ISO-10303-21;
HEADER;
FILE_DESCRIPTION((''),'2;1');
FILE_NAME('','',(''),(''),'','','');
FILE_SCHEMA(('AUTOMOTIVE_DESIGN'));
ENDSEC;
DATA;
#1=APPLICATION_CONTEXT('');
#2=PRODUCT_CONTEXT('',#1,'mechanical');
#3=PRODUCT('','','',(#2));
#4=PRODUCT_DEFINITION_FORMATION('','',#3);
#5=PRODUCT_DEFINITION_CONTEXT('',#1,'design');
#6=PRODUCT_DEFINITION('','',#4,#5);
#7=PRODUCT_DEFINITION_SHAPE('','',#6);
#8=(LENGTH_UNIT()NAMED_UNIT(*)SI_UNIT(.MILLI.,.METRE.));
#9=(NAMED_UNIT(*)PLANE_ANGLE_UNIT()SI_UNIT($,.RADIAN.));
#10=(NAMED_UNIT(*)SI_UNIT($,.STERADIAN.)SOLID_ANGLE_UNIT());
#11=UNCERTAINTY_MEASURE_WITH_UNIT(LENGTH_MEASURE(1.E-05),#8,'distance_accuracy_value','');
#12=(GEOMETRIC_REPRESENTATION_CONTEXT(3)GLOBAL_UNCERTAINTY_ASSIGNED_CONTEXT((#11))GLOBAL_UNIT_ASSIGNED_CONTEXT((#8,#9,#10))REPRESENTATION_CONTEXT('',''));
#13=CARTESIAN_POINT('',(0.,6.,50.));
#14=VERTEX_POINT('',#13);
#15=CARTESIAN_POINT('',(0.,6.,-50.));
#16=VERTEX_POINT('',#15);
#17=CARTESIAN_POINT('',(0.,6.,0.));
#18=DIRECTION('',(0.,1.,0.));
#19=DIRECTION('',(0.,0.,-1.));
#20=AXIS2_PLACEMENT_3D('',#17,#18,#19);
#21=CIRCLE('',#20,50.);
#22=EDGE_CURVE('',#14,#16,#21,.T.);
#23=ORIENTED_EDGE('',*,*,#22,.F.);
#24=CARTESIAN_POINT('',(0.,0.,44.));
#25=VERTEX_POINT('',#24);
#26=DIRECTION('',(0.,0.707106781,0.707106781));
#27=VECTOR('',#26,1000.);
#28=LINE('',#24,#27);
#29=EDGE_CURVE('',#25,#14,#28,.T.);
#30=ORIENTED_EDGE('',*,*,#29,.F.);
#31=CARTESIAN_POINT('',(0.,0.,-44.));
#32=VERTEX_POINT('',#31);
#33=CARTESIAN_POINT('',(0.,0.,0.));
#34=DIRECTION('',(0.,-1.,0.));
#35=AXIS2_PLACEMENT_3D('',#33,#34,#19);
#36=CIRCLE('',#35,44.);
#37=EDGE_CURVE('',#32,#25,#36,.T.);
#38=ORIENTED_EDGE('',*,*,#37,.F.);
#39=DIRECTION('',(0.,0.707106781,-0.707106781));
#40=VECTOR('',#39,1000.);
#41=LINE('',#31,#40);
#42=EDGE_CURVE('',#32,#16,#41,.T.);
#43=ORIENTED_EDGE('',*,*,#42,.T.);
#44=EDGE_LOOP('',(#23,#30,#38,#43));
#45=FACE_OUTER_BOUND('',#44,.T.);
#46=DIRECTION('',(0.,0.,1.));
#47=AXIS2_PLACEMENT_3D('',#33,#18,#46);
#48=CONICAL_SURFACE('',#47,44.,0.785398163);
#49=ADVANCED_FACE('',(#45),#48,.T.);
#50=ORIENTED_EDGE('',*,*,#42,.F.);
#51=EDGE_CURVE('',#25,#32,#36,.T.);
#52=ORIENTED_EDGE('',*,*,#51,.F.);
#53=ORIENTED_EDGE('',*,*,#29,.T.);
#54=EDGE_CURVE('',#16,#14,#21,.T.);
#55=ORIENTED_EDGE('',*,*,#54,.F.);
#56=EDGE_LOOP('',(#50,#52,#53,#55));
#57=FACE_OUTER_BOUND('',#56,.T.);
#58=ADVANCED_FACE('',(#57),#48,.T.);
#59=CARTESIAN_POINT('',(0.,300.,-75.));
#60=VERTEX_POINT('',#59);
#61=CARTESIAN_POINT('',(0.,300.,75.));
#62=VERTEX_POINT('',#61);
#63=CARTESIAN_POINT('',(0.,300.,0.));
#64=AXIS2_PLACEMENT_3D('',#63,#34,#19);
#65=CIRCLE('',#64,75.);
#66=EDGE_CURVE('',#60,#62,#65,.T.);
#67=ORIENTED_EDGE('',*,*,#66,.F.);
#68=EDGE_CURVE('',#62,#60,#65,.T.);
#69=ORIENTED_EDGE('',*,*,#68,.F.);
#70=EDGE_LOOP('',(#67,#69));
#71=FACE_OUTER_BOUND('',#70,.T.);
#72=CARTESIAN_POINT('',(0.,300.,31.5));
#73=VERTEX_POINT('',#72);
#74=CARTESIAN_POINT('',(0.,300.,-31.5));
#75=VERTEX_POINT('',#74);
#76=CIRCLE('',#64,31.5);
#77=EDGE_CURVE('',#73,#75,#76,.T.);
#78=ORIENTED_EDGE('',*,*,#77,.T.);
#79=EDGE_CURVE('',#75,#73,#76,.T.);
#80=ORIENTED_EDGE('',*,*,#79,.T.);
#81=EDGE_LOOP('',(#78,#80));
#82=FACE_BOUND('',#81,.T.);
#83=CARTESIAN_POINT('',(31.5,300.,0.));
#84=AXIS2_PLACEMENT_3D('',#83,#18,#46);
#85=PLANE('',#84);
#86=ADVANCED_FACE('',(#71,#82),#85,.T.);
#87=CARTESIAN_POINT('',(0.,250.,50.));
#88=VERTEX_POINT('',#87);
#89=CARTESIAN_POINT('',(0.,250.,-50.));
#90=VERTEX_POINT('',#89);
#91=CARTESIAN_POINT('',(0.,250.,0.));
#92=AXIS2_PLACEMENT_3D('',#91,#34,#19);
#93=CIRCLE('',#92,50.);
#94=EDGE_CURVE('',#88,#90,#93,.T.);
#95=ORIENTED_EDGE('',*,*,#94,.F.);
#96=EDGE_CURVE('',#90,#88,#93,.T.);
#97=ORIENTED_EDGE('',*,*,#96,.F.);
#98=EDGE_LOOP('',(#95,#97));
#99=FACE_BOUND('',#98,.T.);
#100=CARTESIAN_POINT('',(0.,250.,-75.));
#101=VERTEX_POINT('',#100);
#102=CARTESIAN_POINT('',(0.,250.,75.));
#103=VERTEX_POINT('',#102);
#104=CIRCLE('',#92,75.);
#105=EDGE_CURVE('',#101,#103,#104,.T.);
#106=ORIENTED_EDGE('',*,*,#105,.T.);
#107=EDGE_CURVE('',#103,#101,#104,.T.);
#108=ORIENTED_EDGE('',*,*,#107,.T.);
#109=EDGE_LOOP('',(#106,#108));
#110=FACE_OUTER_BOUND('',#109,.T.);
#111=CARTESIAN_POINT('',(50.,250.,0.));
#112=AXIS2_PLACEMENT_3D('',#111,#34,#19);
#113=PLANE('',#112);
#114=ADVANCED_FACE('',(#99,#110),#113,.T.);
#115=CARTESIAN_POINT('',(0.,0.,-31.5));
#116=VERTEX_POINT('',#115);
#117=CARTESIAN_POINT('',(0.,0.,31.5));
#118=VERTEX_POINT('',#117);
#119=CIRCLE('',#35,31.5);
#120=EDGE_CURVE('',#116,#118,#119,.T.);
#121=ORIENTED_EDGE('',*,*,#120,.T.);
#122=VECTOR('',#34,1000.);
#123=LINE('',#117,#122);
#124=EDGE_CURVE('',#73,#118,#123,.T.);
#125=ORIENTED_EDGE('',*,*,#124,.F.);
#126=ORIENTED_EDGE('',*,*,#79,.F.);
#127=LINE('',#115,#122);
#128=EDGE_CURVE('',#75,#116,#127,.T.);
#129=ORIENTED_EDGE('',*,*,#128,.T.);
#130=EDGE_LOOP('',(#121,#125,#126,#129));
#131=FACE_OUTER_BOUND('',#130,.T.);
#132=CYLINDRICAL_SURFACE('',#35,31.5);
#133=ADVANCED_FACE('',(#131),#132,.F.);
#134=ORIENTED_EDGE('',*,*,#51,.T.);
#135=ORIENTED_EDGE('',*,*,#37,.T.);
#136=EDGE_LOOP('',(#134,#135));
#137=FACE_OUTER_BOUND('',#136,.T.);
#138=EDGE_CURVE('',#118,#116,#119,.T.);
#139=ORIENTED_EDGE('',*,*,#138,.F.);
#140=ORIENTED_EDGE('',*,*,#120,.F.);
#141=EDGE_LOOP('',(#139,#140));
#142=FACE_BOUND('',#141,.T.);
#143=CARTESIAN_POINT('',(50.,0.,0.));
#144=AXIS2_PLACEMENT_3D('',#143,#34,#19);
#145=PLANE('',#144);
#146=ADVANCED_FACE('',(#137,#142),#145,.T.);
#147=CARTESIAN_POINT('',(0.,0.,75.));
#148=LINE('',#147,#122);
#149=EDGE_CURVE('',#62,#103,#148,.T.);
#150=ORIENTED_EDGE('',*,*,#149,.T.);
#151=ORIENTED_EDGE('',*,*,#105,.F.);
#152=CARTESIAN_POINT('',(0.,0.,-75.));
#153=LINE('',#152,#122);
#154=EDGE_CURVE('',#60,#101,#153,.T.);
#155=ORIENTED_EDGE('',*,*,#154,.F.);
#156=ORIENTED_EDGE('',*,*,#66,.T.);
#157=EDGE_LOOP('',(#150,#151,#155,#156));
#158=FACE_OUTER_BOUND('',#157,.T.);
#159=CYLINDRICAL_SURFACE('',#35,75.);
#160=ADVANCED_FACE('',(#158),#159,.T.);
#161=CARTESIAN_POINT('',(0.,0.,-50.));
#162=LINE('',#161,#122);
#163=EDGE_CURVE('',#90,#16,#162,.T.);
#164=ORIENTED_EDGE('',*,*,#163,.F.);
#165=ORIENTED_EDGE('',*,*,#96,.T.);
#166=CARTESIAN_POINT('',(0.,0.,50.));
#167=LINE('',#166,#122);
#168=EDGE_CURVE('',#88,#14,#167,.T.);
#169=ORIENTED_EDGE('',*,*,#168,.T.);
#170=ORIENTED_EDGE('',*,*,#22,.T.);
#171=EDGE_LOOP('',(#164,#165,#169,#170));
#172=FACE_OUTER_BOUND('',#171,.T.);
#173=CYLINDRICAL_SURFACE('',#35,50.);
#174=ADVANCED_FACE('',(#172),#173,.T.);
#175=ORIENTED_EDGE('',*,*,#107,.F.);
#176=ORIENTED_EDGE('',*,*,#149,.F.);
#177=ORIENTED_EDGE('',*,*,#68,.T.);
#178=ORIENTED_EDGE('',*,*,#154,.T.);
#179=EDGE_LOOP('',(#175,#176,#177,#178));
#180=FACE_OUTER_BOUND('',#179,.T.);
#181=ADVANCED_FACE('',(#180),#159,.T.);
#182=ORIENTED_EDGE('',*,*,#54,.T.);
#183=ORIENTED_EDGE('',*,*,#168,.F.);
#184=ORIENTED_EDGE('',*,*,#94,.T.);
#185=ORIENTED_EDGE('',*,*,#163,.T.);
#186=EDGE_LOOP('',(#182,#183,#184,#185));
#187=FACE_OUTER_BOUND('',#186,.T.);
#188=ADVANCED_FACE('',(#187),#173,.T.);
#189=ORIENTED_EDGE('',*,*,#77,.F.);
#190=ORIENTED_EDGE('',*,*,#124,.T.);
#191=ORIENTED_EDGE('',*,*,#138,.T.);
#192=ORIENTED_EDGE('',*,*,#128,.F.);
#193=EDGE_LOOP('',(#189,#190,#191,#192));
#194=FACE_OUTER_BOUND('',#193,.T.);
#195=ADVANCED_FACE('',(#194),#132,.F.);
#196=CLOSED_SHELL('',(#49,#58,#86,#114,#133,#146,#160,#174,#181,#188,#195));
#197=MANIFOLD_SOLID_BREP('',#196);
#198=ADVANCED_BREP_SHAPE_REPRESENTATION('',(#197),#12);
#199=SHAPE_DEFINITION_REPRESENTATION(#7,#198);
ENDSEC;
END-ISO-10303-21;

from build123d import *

# Parameters (mm, degrees)
SHANK_END_CHAMFER_6X45_SIZE = 6


with BuildPart() as part:
    # Pin Profile Sketch → Pin Body Revolve (revolve)
    with BuildSketch(Plane.XY, mode=Mode.PRIVATE) as pin_body_revolve_sk:
        Polygon((50, 0), (50, 250), (75, 250), (75, 300), (31.5, 300), (31.5, 0), align=None)
    revolve(pin_body_revolve_sk.sketch.rotate(Axis((0, 0, 0), (0, 1, 0)), 90), axis=Axis((0, 0, 0), (0, 1, 0)))

    # Shank End Chamfer 6x45°
    shank_end_chamfer_6x45_edges = [part.edges().sort_by_distance(p)[0] for p in [
        (0, 0, 50),
    ]]
    chamfer(shank_end_chamfer_6x45_edges, length=SHANK_END_CHAMFER_6X45_SIZE)


solid = part.part
